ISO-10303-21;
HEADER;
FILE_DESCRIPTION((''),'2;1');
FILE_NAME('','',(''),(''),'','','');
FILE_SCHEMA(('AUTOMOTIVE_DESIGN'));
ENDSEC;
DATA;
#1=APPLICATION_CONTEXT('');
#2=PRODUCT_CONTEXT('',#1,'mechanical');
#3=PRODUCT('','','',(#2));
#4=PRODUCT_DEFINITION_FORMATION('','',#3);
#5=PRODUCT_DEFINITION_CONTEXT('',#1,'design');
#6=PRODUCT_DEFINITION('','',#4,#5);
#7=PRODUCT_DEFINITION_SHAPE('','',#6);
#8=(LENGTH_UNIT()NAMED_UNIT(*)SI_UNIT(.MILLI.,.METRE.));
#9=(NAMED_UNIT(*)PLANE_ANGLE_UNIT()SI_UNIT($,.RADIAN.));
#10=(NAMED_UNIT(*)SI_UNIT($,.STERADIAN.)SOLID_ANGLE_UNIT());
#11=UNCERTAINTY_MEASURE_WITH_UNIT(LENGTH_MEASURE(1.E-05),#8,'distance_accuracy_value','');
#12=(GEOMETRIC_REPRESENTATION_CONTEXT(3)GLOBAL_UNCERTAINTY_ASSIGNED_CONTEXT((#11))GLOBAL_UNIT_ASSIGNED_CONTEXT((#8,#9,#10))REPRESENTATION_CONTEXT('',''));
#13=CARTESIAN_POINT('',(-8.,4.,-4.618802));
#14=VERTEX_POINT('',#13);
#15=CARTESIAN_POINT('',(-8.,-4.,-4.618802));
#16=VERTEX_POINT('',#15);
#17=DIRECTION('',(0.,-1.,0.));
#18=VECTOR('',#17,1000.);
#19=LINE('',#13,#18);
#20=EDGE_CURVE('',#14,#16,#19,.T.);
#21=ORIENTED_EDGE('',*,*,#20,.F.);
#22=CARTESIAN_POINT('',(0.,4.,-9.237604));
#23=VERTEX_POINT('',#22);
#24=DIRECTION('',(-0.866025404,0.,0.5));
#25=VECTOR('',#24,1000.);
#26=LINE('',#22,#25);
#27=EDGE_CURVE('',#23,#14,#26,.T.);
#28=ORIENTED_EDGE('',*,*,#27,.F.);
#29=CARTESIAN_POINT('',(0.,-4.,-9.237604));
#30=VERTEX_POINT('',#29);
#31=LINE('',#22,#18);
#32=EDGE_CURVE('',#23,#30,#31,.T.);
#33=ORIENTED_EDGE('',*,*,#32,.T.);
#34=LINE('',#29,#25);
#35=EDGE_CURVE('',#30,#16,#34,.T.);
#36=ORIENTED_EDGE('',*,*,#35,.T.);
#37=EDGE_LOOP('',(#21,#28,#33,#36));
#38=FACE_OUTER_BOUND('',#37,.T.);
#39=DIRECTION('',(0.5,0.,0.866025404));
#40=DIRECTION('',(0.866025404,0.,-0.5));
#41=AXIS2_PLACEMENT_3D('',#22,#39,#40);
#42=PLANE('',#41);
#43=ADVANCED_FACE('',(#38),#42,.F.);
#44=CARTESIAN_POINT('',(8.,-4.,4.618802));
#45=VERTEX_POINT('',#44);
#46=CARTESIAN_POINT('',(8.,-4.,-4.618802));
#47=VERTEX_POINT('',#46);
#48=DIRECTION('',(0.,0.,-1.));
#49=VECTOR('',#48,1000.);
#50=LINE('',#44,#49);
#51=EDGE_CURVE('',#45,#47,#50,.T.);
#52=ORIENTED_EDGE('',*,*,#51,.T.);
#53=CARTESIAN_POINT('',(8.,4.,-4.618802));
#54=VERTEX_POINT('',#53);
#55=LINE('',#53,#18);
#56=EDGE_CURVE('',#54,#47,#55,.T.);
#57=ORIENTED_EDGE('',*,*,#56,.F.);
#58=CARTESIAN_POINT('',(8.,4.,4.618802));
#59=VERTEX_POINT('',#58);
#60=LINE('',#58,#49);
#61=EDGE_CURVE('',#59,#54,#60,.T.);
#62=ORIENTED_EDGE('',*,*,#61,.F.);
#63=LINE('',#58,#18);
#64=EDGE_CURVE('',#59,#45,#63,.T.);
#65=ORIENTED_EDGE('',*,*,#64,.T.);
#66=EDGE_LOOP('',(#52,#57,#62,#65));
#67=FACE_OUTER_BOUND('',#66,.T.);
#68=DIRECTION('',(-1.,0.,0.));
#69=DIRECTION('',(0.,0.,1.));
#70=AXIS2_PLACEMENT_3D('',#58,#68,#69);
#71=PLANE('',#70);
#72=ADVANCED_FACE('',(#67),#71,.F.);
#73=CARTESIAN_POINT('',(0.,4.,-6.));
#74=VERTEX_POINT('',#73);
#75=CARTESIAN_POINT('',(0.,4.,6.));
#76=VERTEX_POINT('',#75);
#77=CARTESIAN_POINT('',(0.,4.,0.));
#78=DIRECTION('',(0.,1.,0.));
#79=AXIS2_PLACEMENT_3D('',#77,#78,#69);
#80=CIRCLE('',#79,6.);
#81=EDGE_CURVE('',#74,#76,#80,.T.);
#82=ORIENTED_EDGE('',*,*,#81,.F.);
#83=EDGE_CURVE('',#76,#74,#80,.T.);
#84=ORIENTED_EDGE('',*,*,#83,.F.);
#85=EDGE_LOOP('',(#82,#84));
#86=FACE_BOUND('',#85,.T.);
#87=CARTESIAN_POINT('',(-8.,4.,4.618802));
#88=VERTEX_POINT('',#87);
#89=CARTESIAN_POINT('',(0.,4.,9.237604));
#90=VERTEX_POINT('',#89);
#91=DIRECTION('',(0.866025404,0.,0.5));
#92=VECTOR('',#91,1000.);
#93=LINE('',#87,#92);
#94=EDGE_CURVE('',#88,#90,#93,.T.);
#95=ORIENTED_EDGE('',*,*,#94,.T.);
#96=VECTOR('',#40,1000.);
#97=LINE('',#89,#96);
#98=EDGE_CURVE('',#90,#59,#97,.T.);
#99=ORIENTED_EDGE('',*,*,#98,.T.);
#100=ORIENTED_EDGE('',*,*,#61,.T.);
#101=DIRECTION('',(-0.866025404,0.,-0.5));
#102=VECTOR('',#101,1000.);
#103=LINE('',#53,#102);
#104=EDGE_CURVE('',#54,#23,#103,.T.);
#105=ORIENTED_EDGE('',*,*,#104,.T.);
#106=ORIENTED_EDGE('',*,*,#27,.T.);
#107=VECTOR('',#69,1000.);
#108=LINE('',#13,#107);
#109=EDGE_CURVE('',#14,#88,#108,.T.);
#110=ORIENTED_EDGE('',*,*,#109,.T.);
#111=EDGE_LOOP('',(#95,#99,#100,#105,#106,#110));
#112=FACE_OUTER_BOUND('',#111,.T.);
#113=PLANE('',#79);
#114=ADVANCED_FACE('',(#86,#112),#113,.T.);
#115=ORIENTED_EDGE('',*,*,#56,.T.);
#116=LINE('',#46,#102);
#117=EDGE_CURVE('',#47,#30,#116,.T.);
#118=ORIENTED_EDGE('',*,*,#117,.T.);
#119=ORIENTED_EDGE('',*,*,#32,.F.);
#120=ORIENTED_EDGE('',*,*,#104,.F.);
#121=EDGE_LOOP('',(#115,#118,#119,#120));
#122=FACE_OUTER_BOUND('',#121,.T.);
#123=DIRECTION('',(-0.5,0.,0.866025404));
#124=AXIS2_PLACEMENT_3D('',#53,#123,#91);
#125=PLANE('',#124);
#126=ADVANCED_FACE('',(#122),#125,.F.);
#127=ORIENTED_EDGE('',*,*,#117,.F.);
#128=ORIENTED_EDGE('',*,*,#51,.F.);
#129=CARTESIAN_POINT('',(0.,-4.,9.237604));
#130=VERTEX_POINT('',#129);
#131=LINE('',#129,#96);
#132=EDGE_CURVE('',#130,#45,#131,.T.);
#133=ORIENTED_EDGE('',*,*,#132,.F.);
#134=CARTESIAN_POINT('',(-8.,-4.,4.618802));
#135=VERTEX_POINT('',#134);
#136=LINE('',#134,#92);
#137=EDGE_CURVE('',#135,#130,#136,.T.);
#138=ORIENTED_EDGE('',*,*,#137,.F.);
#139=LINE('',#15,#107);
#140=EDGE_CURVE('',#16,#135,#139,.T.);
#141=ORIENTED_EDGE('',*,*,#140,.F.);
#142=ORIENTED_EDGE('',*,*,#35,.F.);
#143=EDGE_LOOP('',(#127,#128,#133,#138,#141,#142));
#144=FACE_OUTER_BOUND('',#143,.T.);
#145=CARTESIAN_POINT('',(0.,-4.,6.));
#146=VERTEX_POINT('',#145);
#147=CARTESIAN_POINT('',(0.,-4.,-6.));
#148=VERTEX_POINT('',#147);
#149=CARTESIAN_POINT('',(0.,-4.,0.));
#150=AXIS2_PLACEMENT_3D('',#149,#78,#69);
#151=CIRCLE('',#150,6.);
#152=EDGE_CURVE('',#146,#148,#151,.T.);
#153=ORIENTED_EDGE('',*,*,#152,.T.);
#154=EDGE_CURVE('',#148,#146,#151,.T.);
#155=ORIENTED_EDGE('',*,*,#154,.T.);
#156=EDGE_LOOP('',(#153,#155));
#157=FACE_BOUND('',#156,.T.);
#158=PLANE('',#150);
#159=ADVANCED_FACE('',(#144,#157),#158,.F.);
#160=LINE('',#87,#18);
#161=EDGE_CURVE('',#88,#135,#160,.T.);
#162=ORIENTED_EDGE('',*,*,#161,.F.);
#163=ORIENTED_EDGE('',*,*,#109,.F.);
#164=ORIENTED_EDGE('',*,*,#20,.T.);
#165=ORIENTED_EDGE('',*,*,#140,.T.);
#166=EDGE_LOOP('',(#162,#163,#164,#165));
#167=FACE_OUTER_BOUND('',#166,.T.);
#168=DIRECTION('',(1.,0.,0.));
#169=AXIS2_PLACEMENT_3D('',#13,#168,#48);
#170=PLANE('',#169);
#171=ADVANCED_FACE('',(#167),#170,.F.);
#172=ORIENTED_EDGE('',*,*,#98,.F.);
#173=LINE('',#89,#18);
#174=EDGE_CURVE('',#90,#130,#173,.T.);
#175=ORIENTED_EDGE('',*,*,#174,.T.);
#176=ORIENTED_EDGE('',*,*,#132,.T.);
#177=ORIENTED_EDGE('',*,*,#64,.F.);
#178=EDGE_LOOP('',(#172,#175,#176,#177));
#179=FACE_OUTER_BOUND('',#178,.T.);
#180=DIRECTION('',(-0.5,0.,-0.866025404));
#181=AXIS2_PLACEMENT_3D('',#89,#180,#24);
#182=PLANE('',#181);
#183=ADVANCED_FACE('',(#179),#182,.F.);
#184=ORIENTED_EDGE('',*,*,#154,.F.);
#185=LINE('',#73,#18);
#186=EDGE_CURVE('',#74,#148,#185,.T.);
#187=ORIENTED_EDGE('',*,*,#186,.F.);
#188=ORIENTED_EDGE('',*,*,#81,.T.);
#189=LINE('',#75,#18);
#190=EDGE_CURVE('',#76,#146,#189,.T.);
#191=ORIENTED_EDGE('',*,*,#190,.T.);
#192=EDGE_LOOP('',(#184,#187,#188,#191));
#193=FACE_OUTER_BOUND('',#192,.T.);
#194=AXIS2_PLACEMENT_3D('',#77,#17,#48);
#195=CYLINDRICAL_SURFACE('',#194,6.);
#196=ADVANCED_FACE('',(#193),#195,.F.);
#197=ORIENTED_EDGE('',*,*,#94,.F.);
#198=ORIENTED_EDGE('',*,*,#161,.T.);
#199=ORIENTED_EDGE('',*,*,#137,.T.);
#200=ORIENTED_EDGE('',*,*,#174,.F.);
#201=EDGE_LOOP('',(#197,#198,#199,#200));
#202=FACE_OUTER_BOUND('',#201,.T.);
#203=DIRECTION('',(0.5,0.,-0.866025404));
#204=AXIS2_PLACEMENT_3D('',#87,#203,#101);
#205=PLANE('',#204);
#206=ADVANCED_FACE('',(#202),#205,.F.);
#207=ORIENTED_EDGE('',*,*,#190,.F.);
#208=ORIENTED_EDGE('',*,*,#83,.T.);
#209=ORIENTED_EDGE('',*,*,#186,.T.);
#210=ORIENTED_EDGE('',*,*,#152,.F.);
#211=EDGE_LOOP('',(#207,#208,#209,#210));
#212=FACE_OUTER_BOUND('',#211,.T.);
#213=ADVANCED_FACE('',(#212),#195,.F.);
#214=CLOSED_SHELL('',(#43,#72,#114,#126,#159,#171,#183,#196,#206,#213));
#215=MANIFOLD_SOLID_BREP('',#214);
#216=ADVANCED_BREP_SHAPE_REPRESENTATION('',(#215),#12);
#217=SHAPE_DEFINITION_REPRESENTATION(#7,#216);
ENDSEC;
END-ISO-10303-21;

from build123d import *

# Parameters (mm, degrees)
HEX_PROFILE_16AF_WITH_BORE_12_R = 6
NUT_BODY_8_MM_DEPTH             = 4


with BuildPart() as part:
    # Hex Profile 16AF with Bore Ø12 → Nut Body 8 mm (new, symmetric)
    with BuildSketch(Plane(origin=(0, 0, 0), x_dir=(1, 0, 0), z_dir=(0, 1, 0))):
        Polygon((0, -9.237604307), (8, -4.618802154), (8, 4.618802154), (0, 9.237604307), (-8, 4.618802154), (-8, -4.618802154), align=None)
        with Locations(Location((0, 0, 0), (0, 0, 270))):
            Circle(HEX_PROFILE_16AF_WITH_BORE_12_R, mode=Mode.SUBTRACT)
    extrude(amount=NUT_BODY_8_MM_DEPTH, both=True)


solid = part.part
